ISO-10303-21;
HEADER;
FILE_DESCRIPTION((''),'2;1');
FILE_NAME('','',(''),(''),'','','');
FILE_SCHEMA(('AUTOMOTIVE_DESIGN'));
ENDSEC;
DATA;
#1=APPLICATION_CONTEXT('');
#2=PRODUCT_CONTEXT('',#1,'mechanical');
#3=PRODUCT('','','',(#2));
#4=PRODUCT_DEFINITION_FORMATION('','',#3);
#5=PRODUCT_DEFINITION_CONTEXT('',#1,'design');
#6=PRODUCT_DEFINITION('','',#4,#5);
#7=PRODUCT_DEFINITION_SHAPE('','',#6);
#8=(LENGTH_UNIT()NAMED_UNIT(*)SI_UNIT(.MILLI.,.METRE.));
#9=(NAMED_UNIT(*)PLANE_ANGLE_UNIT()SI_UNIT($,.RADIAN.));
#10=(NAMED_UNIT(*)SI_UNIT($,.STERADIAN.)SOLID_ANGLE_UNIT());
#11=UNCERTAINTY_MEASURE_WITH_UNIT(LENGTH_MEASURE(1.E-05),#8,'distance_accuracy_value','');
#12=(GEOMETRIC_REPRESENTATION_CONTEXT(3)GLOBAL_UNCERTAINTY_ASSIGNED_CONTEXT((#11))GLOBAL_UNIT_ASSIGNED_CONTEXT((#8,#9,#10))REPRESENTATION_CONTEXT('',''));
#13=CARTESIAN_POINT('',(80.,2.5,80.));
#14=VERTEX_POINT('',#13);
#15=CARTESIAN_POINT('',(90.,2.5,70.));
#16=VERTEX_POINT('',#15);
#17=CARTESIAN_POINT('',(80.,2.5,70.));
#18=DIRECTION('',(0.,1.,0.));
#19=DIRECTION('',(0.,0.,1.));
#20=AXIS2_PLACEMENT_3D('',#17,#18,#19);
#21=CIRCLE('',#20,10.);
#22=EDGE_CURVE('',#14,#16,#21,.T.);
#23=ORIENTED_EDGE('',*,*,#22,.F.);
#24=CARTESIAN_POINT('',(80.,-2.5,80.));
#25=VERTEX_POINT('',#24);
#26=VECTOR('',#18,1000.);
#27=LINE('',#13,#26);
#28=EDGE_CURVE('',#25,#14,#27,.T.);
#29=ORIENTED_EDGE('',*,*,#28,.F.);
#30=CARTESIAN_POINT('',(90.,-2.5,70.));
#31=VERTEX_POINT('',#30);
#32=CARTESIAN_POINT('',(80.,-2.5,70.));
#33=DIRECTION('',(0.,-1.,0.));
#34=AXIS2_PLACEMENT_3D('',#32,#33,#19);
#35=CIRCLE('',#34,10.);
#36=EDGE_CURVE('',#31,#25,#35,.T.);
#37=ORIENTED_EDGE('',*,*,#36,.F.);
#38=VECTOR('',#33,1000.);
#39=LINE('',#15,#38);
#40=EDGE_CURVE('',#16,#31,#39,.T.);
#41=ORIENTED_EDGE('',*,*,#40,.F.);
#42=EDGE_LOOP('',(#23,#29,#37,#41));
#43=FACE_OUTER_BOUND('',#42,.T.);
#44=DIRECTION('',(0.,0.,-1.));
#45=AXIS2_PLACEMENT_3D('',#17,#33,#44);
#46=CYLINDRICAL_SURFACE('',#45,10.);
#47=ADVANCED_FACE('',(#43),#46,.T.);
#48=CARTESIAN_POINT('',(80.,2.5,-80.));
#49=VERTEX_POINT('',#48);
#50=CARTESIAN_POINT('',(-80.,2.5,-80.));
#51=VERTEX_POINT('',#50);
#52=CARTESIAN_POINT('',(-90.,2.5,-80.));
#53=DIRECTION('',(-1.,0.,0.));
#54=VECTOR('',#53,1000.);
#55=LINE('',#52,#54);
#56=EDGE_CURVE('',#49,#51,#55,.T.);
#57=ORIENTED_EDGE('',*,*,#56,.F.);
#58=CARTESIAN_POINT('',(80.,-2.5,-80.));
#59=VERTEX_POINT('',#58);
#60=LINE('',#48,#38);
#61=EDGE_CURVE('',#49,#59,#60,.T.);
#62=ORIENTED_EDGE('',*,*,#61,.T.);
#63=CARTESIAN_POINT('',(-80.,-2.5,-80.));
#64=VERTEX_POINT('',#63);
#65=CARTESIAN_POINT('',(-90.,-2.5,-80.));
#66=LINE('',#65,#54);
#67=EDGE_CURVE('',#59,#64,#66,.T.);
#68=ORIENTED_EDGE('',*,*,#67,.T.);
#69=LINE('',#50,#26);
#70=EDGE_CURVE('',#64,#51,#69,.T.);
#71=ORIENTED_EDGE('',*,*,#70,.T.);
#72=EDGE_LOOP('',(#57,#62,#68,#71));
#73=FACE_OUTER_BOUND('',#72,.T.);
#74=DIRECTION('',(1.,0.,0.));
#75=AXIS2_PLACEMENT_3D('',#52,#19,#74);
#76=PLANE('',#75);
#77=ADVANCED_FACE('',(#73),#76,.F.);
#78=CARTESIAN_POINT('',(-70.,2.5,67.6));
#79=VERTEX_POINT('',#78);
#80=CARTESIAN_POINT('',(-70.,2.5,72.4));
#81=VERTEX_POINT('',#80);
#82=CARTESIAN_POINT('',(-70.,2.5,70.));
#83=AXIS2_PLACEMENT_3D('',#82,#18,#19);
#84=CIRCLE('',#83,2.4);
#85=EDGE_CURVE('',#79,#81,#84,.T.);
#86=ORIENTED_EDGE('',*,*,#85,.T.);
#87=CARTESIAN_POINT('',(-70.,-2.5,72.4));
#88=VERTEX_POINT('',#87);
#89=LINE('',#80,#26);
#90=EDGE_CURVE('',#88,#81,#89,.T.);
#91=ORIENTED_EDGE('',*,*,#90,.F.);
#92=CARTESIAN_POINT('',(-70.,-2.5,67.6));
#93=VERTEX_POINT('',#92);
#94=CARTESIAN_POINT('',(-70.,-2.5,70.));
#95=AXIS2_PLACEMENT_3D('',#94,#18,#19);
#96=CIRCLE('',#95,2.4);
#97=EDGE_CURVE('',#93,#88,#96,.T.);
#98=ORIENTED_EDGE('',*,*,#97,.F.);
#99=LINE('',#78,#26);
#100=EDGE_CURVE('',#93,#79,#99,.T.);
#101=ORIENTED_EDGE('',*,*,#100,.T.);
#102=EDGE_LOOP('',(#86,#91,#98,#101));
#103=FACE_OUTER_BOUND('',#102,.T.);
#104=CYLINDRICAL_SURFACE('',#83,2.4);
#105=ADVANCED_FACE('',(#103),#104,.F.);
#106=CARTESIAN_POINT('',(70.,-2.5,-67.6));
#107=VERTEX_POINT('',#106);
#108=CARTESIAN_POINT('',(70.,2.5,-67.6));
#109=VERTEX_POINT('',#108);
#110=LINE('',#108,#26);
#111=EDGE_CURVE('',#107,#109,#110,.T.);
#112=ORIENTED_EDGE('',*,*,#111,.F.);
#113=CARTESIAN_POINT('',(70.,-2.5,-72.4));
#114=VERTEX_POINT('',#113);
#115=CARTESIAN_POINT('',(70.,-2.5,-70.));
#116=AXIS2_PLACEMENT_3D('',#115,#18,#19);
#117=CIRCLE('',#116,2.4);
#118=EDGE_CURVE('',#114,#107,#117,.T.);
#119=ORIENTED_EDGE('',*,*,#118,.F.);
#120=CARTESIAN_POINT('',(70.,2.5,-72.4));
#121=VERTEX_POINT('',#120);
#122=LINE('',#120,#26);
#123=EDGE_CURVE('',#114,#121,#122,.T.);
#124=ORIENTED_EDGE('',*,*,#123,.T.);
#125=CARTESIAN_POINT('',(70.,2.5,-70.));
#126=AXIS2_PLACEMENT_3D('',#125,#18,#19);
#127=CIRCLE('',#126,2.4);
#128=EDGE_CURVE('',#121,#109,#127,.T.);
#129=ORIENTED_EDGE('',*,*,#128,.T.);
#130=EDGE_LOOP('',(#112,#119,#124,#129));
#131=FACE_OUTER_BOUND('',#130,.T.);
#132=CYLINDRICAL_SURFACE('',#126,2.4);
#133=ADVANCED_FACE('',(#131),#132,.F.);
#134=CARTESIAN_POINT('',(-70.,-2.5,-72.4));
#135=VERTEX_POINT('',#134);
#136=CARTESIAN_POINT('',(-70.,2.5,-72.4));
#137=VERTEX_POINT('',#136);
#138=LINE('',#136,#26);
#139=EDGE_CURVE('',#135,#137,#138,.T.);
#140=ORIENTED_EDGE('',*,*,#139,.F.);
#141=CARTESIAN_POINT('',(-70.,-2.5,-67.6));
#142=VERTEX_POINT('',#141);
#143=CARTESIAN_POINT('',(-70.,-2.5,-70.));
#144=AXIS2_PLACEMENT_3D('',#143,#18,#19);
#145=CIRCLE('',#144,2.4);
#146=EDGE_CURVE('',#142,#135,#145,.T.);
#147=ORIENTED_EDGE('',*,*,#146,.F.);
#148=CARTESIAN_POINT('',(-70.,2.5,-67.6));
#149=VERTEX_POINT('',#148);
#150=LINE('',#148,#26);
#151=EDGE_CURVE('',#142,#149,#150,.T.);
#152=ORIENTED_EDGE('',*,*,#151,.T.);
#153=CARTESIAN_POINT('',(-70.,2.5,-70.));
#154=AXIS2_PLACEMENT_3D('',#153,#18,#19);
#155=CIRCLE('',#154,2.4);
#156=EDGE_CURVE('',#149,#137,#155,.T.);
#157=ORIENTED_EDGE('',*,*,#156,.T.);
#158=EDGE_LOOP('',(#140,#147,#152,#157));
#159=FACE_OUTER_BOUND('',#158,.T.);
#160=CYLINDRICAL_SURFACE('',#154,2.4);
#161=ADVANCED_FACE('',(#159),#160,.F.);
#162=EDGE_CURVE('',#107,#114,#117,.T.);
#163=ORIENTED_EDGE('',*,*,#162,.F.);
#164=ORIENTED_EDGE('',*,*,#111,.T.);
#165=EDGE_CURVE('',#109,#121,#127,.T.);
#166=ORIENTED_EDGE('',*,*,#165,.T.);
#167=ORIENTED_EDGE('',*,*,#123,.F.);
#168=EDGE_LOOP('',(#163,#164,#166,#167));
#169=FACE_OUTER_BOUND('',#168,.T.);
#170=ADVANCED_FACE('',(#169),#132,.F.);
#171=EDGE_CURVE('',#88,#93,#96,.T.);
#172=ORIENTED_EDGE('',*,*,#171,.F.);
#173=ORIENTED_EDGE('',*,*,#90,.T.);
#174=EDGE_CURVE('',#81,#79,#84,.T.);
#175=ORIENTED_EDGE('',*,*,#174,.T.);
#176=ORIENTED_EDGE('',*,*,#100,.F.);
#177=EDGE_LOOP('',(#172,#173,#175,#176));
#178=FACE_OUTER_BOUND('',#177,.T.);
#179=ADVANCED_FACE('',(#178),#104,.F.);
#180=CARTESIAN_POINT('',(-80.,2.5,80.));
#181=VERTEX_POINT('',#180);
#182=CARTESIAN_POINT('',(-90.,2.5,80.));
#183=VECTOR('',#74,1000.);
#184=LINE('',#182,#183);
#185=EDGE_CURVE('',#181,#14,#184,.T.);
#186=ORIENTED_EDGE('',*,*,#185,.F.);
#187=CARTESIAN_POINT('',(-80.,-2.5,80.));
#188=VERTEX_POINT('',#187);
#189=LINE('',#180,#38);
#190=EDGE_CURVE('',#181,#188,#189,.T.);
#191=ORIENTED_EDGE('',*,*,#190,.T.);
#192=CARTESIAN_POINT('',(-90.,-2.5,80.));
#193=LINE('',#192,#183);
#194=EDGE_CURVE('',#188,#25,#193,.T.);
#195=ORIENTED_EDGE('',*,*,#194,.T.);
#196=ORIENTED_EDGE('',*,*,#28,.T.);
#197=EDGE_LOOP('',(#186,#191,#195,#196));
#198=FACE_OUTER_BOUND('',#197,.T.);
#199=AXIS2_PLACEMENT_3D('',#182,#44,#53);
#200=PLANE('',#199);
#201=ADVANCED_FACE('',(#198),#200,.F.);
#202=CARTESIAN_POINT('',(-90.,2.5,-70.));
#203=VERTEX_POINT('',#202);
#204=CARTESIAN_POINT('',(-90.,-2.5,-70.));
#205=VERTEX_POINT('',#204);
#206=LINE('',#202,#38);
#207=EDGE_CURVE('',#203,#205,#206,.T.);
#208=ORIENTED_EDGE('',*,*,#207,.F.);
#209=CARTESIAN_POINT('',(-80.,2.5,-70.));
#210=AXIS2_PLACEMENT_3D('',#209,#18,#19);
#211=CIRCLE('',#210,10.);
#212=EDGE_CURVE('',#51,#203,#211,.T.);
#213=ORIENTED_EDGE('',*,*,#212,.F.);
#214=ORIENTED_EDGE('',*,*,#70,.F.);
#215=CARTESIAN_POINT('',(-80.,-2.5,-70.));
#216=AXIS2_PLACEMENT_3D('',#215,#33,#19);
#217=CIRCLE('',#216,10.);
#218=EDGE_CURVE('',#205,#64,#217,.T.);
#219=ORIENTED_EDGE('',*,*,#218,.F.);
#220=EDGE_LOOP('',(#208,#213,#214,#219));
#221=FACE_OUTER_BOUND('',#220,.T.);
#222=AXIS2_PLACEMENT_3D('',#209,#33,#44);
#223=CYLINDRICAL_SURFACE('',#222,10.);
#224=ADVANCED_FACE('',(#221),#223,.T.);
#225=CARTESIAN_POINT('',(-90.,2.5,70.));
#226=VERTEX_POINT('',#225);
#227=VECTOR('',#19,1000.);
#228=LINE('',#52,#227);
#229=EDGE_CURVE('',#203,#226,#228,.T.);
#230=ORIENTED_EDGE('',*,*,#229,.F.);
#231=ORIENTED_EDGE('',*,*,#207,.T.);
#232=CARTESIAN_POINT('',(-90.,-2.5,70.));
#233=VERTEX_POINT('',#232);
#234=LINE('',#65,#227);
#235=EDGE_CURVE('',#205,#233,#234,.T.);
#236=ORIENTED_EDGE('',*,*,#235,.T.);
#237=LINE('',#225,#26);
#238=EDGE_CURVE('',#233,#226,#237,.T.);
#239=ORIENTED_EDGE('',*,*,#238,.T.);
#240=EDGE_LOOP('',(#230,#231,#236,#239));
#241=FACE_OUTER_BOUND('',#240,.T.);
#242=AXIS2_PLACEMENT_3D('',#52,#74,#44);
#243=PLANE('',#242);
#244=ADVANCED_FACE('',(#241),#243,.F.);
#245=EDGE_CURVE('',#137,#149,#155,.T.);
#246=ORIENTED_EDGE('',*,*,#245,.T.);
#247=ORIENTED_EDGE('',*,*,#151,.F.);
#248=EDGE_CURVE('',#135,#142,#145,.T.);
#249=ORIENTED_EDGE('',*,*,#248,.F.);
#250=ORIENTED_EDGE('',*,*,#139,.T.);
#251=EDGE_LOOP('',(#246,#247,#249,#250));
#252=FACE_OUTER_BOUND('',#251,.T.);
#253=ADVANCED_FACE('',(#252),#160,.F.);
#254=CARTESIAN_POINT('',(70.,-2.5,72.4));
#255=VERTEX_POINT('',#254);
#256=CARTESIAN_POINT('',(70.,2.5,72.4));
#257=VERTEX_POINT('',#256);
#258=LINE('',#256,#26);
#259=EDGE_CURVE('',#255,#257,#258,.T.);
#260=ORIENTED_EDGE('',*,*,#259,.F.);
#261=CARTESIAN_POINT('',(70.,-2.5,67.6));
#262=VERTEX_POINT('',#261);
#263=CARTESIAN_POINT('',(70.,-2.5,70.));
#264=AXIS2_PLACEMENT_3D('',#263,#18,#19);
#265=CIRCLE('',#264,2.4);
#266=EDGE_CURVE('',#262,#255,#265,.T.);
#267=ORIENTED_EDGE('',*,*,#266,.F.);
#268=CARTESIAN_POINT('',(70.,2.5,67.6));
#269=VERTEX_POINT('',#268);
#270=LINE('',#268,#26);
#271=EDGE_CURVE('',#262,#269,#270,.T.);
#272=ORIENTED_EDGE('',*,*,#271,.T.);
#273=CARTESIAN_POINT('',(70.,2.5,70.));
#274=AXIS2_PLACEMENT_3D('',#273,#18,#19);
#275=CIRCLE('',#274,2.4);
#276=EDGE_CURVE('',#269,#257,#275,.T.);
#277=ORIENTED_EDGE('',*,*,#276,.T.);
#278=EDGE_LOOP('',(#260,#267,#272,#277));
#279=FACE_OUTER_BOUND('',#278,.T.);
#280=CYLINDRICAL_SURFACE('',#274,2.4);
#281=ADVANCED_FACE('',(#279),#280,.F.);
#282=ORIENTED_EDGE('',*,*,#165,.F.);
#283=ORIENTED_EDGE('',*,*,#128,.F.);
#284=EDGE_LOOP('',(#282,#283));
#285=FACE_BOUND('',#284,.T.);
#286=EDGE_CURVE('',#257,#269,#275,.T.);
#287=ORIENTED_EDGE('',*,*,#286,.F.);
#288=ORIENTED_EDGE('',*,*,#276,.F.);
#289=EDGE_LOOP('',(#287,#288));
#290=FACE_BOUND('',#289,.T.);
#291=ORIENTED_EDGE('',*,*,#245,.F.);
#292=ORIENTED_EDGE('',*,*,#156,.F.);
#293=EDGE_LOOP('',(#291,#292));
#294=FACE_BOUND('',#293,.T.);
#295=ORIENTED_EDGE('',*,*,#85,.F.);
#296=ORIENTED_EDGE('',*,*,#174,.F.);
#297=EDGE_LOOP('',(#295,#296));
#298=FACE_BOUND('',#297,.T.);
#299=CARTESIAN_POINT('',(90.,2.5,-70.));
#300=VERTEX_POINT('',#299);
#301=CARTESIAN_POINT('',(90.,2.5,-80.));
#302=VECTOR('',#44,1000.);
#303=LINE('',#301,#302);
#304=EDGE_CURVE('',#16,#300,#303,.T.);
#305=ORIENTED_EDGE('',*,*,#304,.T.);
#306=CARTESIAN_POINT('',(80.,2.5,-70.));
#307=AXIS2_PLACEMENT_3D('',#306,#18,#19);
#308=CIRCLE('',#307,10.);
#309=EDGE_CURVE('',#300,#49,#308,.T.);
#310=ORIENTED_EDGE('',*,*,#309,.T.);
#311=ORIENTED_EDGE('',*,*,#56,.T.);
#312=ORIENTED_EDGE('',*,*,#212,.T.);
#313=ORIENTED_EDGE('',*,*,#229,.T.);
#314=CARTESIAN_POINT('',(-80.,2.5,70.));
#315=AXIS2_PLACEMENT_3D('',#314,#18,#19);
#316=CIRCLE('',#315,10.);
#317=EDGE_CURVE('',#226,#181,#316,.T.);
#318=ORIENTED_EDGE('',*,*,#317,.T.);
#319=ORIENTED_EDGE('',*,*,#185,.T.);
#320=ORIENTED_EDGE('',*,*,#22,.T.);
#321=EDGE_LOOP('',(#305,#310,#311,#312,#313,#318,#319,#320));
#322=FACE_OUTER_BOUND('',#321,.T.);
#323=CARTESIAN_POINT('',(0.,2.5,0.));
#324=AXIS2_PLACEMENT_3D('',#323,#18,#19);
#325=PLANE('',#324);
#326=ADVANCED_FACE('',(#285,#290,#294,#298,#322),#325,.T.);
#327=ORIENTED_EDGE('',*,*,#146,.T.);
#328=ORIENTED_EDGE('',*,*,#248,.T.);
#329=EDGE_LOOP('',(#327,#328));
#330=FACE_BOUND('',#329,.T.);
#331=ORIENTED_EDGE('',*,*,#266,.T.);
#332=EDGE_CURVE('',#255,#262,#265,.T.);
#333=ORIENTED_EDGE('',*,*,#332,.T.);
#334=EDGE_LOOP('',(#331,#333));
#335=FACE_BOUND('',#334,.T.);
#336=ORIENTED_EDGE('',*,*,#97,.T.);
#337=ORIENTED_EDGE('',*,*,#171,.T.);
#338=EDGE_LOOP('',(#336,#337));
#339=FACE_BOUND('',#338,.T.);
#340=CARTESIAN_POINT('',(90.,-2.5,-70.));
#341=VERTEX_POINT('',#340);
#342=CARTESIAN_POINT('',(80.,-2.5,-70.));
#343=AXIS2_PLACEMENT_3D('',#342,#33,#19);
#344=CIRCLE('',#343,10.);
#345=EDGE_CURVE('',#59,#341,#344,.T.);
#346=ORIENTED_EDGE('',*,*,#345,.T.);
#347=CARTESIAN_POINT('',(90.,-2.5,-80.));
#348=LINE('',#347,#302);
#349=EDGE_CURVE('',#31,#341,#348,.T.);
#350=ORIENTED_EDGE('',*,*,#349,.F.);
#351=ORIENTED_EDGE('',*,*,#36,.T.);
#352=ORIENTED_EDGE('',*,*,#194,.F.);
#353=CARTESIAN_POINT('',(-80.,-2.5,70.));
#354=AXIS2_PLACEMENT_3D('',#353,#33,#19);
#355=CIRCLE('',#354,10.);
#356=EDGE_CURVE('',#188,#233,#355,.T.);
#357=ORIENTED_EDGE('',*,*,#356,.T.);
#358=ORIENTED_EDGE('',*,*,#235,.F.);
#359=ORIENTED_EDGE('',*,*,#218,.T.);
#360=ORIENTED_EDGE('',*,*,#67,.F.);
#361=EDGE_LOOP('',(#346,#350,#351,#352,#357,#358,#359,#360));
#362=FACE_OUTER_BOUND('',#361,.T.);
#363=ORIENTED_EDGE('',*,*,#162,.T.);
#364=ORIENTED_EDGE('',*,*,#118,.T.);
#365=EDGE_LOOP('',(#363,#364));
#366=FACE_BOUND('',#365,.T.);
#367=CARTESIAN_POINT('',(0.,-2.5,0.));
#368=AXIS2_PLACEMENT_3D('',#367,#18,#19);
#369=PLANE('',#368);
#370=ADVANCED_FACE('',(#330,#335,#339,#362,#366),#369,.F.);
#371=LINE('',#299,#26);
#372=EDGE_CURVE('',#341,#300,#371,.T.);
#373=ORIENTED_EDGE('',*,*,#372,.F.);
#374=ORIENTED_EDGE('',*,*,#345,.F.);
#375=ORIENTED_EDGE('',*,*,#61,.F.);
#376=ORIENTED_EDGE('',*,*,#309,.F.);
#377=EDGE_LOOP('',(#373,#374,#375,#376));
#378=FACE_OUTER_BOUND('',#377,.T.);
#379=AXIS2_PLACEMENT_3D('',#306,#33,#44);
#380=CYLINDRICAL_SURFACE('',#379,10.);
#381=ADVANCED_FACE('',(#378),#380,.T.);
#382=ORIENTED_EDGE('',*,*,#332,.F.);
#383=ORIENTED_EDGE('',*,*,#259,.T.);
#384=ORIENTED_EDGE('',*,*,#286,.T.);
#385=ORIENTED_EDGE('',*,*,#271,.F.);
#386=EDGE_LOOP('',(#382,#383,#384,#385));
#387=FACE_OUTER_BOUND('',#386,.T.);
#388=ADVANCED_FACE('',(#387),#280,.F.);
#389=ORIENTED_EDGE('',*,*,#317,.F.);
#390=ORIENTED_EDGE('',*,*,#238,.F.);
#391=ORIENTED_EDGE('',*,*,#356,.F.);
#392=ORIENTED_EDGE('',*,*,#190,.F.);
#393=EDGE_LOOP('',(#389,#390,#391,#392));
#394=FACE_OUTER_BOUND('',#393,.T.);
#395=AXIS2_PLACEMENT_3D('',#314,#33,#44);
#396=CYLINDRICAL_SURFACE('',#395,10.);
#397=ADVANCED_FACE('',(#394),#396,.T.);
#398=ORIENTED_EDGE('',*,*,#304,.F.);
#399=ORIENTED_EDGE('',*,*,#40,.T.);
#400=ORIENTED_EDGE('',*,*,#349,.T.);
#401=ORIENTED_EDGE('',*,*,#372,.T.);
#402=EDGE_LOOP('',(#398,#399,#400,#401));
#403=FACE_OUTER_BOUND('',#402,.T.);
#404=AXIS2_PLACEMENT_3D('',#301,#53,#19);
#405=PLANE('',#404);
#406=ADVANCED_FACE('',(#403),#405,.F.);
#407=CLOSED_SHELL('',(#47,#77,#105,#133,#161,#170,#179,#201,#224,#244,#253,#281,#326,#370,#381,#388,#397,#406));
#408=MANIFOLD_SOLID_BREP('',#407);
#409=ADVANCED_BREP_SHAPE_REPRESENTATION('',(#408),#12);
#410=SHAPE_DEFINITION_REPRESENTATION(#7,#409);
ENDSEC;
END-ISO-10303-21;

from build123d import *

# Parameters (mm, degrees)
SKETCH1_W            = 180
SKETCH1_H            = 160
BOSS_EXTRUDE1_DEPTH  = 2.5
M4_CLEARANCE_HOLE1_D = 4.8
FILLET1_R            = 10


with BuildPart() as part:
    # Sketch1 → Boss-Extrude1 (new, symmetric)
    with BuildSketch(Plane(origin=(0, 0, 0), x_dir=(1, 0, 0), z_dir=(0, 1, 0))):
        Rectangle(SKETCH1_W, SKETCH1_H)
    extrude(amount=BOSS_EXTRUDE1_DEPTH, both=True)

    # M4 Clearance Hole1 (through all)
    with Locations(Plane(origin=(-70, 2.5, -70), x_dir=(0, 0, 1), z_dir=(0, 1, 0))):
        with Locations((0, 0), (0, 140), (140, 140), (140, 0)):
            Hole(M4_CLEARANCE_HOLE1_D / 2)

    # Fillet1
    fillet1_edges = [part.edges().sort_by_distance(p)[0] for p in [
        (90, 0, 80),
        (-90, 0, 80),
        (-90, 0, -80),
        (90, 0, -80),
    ]]
    fillet(fillet1_edges, radius=FILLET1_R)


solid = part.part
